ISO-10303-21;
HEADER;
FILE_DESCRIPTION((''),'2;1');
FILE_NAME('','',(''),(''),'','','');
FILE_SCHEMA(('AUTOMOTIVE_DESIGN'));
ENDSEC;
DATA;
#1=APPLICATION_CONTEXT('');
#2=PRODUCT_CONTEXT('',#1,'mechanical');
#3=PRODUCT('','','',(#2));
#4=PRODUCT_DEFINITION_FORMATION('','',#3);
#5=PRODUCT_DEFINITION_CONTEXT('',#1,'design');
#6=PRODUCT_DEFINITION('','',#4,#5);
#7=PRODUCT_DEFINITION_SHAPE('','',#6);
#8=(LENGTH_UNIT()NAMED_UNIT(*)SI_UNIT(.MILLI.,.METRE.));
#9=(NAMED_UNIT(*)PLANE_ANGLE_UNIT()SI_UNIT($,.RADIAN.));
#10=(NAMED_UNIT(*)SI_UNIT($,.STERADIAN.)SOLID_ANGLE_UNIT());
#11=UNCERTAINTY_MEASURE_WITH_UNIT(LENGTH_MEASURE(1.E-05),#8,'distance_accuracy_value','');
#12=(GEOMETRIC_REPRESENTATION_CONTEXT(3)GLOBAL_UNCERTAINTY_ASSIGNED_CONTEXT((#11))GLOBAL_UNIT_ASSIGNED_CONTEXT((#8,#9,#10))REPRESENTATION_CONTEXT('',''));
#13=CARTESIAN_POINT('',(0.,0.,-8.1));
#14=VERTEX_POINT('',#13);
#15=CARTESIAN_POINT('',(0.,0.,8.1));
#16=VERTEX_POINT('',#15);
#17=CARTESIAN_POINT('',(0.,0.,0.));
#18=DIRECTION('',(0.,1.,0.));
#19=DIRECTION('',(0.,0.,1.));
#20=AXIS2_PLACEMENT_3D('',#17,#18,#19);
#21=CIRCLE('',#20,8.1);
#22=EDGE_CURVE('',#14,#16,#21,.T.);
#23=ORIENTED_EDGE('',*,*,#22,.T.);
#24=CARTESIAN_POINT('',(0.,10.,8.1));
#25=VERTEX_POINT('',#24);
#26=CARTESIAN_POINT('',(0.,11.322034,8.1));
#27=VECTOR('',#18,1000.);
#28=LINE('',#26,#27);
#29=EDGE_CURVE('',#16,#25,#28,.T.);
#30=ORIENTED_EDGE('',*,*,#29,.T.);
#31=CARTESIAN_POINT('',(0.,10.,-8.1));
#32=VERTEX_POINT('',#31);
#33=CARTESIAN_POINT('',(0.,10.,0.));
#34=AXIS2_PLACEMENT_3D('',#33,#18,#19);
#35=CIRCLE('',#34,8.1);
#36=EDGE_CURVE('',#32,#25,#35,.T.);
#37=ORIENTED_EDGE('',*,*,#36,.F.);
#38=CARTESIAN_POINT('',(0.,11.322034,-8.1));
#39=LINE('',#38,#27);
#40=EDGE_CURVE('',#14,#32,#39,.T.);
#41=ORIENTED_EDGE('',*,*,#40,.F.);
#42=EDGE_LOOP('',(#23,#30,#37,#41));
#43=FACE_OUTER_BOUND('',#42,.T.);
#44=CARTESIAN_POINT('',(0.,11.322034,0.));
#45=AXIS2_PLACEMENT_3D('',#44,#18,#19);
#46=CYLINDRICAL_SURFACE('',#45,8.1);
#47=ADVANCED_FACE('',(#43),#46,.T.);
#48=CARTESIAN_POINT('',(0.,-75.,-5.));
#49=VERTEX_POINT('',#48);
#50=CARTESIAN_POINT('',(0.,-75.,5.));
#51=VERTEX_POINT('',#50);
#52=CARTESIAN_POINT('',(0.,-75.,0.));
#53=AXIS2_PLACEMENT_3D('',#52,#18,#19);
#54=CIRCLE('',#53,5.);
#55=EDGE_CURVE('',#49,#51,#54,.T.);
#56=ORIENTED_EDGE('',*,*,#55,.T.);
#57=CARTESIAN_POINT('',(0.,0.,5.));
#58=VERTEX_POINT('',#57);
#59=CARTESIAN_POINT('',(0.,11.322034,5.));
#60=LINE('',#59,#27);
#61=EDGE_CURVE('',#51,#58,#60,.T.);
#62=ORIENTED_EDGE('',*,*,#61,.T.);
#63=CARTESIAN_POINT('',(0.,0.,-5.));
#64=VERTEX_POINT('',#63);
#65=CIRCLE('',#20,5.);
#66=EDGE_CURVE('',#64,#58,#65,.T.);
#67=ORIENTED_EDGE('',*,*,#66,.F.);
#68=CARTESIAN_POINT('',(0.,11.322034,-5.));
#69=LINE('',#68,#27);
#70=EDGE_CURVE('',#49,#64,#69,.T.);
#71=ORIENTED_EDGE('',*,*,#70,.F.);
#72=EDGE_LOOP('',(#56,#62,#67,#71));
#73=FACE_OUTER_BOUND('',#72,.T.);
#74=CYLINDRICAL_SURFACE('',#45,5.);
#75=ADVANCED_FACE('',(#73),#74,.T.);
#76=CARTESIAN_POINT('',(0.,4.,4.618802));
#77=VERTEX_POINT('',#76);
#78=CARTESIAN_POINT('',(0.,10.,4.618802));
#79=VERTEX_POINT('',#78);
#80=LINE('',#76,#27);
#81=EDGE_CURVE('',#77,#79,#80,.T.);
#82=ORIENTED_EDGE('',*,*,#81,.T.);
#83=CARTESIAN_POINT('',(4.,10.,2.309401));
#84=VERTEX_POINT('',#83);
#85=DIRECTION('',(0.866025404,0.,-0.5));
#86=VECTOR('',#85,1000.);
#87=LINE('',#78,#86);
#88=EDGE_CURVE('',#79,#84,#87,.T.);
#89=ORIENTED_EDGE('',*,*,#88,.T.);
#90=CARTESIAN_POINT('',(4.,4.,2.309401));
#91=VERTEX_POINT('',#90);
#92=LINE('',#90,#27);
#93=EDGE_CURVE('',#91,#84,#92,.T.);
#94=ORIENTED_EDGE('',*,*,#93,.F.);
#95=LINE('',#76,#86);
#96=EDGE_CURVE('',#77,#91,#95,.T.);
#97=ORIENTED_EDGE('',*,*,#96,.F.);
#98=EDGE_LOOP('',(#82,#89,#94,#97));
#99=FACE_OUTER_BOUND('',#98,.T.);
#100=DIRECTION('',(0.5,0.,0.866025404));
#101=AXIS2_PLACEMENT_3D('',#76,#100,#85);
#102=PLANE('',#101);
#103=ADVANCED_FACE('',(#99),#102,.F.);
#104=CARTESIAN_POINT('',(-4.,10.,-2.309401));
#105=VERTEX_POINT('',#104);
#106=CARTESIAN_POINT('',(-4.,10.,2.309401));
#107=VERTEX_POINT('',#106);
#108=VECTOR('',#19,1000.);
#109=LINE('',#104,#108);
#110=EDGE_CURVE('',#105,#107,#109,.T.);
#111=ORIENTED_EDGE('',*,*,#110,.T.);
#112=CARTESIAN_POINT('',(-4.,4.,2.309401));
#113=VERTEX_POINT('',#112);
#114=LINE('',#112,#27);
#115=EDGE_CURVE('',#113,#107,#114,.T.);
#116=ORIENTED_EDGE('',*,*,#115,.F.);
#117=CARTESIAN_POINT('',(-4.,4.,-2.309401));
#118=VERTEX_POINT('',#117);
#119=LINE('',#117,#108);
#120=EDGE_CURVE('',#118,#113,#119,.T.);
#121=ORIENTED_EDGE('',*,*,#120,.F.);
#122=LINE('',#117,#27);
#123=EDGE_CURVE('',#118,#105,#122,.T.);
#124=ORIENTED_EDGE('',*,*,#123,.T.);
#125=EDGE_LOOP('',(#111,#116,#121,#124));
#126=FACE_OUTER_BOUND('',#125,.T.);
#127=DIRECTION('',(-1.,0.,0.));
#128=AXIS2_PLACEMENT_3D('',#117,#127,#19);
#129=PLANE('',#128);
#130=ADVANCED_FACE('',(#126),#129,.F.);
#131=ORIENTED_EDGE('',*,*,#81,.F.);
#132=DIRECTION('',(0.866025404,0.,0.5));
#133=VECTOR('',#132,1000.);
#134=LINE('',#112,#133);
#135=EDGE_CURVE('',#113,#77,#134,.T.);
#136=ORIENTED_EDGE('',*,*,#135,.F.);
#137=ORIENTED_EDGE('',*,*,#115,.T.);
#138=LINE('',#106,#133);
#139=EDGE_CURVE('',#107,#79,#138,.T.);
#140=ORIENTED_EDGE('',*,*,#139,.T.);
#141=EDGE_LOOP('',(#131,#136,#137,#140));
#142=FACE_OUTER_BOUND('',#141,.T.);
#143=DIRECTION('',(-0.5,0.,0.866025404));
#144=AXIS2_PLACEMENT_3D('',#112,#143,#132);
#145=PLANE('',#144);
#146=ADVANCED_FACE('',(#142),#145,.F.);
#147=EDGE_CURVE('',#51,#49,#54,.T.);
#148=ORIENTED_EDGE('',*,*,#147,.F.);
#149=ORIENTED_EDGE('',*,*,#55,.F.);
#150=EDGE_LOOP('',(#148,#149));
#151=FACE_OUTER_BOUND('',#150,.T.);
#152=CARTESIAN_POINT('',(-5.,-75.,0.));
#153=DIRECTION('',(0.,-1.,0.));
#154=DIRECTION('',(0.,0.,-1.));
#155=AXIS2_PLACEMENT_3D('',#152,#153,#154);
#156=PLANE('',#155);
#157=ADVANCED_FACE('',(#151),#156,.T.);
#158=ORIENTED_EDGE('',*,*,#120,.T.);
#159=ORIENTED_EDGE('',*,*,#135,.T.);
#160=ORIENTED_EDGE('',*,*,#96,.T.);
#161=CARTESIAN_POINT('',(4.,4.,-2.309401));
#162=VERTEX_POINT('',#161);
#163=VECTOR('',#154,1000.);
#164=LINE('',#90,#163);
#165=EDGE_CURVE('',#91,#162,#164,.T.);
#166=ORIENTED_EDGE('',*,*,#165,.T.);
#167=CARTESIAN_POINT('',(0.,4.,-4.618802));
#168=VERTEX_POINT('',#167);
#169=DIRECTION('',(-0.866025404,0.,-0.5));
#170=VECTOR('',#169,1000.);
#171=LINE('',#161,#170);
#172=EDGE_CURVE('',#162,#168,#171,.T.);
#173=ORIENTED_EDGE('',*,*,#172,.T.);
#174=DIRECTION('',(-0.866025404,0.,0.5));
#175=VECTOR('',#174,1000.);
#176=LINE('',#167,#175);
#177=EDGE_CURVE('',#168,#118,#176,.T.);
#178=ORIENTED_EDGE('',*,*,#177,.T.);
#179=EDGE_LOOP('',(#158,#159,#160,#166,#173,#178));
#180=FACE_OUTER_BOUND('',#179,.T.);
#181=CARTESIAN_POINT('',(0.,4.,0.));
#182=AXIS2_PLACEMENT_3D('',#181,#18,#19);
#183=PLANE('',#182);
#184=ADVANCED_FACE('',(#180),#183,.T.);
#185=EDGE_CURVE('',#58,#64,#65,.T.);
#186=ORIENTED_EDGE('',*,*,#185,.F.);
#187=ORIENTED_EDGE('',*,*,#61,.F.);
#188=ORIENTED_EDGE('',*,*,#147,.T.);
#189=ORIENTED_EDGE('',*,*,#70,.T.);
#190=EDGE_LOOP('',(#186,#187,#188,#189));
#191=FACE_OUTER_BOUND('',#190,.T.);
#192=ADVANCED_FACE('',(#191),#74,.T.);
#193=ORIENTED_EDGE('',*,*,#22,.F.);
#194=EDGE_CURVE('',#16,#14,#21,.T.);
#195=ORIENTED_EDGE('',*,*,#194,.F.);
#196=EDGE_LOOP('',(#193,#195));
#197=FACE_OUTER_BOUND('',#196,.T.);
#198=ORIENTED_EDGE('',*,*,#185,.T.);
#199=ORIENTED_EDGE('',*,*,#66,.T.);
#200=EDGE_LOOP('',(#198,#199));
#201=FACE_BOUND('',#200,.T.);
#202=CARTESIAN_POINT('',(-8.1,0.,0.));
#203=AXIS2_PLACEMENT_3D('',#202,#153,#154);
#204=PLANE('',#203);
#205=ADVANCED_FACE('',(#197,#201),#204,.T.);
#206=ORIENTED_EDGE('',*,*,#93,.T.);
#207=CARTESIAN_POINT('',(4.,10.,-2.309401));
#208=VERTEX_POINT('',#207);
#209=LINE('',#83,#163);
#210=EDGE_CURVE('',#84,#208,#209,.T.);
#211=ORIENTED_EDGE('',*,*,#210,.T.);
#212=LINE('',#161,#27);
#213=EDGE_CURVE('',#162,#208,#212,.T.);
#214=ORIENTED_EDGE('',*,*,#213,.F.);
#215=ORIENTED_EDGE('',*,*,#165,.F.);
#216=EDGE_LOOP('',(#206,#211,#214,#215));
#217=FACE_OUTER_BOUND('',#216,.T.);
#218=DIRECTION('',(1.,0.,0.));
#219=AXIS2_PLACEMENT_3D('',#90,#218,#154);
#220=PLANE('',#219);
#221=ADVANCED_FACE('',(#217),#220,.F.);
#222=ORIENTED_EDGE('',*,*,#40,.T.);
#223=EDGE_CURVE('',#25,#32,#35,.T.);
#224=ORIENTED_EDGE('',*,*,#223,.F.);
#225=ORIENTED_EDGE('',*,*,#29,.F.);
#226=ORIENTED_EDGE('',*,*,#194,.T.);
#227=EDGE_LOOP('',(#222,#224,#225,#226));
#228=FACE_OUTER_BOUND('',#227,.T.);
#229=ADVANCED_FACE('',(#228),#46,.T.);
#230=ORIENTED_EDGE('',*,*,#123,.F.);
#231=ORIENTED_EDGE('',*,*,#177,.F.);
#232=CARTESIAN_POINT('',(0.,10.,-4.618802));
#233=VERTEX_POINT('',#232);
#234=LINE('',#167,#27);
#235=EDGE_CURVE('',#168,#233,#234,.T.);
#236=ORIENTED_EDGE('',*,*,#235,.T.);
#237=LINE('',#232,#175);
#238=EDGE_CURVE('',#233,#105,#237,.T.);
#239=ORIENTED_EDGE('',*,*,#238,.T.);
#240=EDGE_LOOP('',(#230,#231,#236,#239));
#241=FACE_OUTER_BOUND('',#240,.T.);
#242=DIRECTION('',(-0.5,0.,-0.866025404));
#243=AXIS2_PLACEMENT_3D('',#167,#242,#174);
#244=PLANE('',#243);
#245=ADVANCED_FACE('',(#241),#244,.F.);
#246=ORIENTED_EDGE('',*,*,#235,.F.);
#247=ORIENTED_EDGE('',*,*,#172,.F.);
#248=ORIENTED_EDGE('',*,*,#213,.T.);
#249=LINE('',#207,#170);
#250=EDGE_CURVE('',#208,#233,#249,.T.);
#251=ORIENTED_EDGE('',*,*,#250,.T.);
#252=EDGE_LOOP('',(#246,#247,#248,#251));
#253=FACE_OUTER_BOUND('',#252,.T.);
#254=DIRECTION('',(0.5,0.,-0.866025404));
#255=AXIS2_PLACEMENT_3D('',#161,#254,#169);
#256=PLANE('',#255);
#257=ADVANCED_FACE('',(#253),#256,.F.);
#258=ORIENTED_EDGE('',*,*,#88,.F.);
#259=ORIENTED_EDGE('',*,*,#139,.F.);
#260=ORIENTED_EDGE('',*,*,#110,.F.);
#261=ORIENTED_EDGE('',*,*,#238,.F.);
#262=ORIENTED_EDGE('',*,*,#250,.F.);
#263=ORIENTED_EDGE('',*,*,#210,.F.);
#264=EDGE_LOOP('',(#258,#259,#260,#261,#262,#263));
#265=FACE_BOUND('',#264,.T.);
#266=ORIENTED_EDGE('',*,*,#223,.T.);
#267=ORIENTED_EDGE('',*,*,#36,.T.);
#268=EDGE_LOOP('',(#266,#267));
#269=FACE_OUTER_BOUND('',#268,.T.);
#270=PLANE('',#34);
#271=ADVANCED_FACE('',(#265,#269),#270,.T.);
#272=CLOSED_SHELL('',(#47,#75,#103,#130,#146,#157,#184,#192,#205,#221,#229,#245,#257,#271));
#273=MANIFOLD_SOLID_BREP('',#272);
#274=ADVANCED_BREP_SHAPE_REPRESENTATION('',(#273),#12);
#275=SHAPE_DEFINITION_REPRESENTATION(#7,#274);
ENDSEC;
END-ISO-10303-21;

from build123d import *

# Parameters (mm, degrees)
CUT_EXTRUDE_1_DEPTH = 6


with BuildPart() as part:
    # Sketch 1 → Revolve 1 (revolve)
    with BuildSketch(Plane.XY, mode=Mode.PRIVATE) as revolve_1_sk:
        Polygon((0, 10), (-8.1, 10), (-8.1, 0), (-5, 0), (-5, -75), (0, -75), align=None)
    revolve(revolve_1_sk.sketch.rotate(Axis((0, 11.322033898, 0), (0, -1, 0)), 270), axis=Axis((0, 11.322033898, 0), (0, -1, 0)))

    # Sketch 2 → Cut-Extrude 1 (cut)
    with BuildSketch(Plane(origin=(0, 10, 0), x_dir=(1, 0, 0), z_dir=(0, 1, 0))):
        Polygon((0, 4.618802154), (-4, 2.309401077), (-4, -2.309401077), (0, -4.618802154), (4, -2.309401077), (4, 2.309401077), align=None)
    extrude(amount=-CUT_EXTRUDE_1_DEPTH, mode=Mode.SUBTRACT)


solid = part.part
